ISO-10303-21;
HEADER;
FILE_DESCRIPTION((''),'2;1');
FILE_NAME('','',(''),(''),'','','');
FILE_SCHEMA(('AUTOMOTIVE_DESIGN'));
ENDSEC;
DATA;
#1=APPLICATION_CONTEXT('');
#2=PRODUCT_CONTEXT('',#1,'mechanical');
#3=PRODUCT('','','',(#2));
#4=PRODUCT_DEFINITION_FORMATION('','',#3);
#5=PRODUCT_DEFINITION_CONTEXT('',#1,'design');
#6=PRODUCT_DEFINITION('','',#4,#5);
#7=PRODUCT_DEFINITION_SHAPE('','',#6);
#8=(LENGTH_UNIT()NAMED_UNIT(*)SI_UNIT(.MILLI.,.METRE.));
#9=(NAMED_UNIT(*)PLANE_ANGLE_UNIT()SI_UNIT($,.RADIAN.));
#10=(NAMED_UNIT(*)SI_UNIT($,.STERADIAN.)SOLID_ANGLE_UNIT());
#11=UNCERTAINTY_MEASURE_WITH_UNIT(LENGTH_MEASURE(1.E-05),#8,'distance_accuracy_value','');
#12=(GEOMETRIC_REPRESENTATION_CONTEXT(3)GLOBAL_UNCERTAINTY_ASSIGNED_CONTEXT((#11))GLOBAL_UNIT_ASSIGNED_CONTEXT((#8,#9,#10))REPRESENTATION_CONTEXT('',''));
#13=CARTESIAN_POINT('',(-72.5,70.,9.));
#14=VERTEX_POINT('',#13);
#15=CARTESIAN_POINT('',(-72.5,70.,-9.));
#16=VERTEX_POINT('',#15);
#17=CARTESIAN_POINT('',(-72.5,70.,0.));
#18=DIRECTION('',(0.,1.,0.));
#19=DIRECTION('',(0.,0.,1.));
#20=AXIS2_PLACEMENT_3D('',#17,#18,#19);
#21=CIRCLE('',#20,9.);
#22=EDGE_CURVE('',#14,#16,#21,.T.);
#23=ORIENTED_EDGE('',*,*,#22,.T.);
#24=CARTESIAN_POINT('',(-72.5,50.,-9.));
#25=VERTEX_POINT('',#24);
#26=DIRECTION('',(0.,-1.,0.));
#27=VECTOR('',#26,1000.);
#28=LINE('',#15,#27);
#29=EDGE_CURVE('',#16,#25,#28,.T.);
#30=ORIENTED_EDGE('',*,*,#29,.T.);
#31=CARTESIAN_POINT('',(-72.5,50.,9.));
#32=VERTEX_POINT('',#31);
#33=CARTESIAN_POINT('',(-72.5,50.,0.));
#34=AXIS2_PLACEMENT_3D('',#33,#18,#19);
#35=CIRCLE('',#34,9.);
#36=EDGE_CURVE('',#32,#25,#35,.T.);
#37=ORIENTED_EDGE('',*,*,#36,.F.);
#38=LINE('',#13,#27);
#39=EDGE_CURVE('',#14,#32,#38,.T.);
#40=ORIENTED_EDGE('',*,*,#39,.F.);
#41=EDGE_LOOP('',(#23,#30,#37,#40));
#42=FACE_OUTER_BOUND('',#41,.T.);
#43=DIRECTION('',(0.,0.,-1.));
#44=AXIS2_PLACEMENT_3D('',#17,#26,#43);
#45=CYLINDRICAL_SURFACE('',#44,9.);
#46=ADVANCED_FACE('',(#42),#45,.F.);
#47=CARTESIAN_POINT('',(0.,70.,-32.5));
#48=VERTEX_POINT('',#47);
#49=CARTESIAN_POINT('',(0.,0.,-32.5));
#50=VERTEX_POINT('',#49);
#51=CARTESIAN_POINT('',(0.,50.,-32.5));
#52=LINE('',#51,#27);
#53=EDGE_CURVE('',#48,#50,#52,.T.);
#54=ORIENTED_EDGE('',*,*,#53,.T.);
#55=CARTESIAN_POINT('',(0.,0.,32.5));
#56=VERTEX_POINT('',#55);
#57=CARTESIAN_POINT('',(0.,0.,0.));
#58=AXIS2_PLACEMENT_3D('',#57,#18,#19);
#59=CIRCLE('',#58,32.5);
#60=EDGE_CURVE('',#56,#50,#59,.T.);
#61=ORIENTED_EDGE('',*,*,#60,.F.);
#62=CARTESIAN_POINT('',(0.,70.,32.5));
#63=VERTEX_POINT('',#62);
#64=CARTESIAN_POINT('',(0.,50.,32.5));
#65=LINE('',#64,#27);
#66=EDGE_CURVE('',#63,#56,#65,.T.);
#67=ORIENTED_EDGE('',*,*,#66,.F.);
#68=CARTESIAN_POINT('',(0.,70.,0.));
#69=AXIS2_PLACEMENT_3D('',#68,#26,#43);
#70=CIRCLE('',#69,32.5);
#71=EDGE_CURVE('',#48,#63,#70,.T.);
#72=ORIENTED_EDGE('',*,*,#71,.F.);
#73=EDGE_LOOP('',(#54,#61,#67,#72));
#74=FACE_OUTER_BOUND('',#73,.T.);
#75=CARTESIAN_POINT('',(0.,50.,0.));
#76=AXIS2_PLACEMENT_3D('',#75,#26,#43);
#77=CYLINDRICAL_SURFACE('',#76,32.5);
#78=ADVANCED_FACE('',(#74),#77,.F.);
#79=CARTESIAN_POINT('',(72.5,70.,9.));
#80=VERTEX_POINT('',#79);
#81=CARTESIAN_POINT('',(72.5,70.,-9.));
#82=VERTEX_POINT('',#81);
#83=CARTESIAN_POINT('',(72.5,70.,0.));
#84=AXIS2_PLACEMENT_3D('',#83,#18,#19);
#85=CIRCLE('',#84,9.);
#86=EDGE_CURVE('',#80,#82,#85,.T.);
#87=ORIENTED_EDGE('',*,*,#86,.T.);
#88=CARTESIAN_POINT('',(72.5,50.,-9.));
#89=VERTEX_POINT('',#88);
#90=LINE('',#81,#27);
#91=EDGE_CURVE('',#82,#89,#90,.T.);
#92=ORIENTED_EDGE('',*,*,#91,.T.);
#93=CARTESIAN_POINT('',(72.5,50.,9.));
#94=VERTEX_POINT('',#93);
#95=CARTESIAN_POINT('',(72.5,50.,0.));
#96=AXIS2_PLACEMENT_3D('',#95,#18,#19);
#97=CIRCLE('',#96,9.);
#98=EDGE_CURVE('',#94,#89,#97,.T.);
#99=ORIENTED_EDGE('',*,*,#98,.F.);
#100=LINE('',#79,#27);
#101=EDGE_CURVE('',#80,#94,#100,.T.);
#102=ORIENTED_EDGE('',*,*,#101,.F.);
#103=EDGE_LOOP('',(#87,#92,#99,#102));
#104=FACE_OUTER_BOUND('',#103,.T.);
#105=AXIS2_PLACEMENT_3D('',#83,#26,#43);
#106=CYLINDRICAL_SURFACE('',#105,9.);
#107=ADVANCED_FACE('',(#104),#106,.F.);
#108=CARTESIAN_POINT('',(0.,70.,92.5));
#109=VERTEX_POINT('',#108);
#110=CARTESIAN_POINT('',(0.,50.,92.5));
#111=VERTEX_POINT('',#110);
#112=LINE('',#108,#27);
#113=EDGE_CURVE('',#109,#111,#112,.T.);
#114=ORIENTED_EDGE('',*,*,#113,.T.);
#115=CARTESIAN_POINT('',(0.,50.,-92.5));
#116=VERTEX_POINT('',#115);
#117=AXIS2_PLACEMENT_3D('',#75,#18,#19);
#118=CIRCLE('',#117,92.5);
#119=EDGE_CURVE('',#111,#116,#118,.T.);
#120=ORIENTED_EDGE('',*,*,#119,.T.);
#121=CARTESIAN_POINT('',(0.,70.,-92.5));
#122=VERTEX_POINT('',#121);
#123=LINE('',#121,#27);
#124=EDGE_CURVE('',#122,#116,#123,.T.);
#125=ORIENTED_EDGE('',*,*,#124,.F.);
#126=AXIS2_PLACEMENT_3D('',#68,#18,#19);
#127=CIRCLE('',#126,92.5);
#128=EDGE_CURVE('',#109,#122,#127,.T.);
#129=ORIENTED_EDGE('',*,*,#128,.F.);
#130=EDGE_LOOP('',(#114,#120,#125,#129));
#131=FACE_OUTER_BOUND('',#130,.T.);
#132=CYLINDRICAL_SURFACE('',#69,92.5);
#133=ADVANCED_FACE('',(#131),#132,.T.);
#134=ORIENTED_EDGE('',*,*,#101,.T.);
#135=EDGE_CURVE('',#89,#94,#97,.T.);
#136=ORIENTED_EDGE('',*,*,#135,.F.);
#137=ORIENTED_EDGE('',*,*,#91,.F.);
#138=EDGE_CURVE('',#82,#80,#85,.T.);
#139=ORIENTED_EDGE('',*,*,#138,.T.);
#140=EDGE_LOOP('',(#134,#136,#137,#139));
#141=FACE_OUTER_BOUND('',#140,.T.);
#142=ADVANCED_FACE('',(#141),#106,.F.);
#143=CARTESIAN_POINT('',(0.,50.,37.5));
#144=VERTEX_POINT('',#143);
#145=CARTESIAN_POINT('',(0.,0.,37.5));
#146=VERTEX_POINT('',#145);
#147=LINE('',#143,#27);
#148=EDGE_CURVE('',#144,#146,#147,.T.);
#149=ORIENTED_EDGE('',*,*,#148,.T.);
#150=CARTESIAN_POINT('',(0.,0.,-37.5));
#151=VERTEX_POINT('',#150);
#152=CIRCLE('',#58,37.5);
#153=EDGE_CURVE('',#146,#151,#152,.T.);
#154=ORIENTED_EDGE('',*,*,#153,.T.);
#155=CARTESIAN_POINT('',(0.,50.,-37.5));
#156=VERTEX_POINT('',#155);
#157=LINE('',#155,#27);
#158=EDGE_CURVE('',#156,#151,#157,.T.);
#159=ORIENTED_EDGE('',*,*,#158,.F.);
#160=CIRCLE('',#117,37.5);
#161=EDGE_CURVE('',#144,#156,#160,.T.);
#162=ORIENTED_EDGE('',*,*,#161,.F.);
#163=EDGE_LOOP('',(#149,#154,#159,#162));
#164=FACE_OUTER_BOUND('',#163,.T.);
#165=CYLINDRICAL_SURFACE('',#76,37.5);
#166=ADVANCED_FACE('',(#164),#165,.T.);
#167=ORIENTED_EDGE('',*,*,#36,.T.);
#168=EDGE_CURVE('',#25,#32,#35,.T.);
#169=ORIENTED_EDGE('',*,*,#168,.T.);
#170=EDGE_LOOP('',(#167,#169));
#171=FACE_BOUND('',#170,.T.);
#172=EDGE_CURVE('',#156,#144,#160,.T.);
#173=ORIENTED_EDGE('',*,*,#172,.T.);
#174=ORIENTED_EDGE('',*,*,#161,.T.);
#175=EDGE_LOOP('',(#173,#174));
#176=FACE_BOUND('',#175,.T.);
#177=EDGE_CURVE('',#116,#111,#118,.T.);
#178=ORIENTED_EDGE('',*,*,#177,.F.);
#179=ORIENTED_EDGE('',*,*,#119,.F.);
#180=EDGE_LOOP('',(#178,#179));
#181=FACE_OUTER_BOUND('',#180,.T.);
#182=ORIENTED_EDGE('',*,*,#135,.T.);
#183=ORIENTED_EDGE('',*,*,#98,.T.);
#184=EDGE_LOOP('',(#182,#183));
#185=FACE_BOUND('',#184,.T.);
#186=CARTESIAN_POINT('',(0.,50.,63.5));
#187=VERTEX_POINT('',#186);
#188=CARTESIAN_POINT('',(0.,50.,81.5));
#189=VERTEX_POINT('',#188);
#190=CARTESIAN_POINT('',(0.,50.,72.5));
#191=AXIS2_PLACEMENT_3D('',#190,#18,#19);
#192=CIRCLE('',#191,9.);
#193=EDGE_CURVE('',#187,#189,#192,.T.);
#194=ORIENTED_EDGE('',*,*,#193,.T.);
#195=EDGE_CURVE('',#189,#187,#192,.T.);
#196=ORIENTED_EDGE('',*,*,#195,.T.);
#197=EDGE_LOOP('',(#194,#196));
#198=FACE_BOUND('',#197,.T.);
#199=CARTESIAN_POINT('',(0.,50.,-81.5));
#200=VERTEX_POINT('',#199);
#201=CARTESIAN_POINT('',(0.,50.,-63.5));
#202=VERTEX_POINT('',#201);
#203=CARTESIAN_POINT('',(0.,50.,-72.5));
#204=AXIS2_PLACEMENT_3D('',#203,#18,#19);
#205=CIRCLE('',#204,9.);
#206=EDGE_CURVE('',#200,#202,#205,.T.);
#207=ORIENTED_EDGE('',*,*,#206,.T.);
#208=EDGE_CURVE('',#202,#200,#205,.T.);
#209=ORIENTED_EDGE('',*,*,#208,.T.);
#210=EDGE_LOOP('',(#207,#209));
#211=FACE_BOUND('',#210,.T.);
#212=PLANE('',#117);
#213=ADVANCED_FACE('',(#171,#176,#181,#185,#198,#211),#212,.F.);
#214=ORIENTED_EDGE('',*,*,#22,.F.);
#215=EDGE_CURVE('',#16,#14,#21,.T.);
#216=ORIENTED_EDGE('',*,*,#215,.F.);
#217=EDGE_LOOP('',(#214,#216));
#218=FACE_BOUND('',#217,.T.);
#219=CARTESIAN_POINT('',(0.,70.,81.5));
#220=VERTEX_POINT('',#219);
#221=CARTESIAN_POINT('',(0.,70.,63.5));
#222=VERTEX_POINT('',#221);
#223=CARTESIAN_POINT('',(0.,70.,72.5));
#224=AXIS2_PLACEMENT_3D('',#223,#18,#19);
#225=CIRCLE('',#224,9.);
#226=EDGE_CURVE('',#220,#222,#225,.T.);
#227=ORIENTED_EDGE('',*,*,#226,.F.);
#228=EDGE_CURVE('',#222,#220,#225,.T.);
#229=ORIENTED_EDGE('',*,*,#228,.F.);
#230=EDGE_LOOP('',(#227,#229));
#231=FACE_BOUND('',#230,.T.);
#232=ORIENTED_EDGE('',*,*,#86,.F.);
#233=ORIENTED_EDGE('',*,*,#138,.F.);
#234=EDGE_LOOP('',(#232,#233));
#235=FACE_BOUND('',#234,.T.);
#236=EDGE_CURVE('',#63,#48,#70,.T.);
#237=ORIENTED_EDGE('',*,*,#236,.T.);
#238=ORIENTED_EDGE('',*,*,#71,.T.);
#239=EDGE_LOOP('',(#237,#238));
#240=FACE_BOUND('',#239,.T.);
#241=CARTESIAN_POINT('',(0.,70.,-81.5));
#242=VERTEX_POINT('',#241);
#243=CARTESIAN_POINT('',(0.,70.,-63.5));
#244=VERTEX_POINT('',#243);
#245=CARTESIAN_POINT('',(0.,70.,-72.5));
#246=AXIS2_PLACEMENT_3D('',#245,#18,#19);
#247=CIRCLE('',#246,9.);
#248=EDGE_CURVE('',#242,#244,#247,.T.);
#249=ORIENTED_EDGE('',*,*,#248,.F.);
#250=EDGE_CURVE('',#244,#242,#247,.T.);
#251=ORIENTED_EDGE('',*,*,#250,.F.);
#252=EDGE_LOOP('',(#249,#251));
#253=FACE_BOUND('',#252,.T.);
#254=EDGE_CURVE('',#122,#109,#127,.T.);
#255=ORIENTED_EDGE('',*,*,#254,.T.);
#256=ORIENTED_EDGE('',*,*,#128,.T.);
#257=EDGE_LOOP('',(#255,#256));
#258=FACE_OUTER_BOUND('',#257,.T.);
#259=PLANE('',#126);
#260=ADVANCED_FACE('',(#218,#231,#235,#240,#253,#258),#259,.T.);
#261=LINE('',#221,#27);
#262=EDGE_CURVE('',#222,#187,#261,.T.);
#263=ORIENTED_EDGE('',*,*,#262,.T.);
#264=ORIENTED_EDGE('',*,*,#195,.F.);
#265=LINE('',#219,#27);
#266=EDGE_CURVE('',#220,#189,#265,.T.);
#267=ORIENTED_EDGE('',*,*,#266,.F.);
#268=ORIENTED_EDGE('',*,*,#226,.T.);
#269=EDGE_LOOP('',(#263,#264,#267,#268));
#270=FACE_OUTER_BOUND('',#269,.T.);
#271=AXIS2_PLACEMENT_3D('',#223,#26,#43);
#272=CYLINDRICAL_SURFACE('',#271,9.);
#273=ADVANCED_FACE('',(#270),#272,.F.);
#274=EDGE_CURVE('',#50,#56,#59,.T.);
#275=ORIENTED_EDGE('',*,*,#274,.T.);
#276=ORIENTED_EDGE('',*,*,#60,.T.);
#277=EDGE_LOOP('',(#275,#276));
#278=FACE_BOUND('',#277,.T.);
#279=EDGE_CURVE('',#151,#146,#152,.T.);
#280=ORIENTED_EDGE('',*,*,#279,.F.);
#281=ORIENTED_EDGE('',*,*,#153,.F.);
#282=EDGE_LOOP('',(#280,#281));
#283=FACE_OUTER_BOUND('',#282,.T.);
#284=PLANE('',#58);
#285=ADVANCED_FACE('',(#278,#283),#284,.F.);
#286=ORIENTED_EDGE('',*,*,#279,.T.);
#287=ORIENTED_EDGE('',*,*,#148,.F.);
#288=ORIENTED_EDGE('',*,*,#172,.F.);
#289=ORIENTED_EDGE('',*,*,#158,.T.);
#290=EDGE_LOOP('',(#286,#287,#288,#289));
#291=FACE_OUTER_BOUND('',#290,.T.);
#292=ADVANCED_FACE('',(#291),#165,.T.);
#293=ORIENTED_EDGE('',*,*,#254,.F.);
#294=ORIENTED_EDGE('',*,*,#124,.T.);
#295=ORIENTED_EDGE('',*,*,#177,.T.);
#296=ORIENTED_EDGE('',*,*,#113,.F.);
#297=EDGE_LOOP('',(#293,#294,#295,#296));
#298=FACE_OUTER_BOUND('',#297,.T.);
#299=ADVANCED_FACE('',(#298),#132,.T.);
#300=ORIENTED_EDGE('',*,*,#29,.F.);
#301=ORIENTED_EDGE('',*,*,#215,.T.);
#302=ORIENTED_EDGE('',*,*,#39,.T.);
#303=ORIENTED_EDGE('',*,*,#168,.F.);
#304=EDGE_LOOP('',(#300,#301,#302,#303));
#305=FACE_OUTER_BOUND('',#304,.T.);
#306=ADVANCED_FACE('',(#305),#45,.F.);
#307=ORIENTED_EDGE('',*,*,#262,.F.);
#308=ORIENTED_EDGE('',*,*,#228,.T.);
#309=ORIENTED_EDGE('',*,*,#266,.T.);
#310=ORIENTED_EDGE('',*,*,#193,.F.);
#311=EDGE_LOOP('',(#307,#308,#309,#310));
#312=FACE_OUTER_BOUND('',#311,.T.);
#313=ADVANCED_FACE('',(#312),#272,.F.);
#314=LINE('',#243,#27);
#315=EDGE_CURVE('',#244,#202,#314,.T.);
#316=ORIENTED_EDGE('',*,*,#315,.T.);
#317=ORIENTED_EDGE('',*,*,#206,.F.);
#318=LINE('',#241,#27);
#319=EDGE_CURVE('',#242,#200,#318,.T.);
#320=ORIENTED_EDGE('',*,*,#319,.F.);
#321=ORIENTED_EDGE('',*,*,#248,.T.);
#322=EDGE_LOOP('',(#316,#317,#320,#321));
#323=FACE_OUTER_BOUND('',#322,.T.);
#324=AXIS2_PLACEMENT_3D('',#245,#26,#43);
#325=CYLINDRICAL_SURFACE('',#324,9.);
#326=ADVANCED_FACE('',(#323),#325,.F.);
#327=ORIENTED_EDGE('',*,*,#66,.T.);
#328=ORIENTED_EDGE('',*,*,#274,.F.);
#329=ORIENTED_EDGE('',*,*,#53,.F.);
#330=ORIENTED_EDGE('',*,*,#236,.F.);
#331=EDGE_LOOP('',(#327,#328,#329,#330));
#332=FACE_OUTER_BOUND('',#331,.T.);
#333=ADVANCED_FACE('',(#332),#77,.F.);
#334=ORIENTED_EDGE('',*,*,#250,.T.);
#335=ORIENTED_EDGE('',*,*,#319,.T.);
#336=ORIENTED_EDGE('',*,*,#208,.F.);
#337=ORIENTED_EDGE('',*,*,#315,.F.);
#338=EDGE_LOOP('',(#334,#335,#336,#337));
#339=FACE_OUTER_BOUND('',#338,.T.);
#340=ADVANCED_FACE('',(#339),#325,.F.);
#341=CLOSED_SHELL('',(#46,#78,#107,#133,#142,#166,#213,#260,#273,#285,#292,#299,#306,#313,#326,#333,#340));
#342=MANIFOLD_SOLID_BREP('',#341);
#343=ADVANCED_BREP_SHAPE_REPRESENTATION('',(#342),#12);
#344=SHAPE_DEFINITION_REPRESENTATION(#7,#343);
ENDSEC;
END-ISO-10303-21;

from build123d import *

# Parameters (mm, degrees)
SKETCH_1_R          = 37.5
SKETCH_1_R_2        = 32.5
EXTRUDE_1_DEPTH     = 50
SKETCH_2_R          = 92.5
SKETCH_2_R_2        = 37.5
SKETCH_2_R_3        = 9
EXTRUDE_2_DEPTH     = 20
SKETCH_3_R          = 37.5
EXTRUDE_3_DEPTH     = 20
SKETCH_4_R          = 32.5
CUT_EXTRUDE_1_DEPTH = 141.044635742


with BuildPart() as part:
    # 草图1 → 凸台-拉伸1 (new body)
    with BuildSketch(Plane(origin=(0, 0, 0), x_dir=(1, 0, 0), z_dir=(0, 1, 0))):
        with Locations(Location((0, 0, 0), (0, 0, 270))):
            Circle(SKETCH_1_R)
        with Locations(Location((0, 0, 0), (0, 0, 270))):
            Circle(SKETCH_1_R_2, mode=Mode.SUBTRACT)
    extrude(amount=EXTRUDE_1_DEPTH)



with BuildPart() as body_2:
    # 草图2 → 凸台-拉伸2 (new body)
    with BuildSketch(Plane(origin=(0, 50, 0), x_dir=(1, 0, 0), z_dir=(0, 1, 0))):
        with Locations(Location((0, 0, 0), (0, 0, 270))):
            Circle(SKETCH_2_R)
        with Locations(Location((0, 0, 0), (0, 0, 270))):
            Circle(SKETCH_2_R_2, mode=Mode.SUBTRACT)
        with Locations(Location((-72.5, 0, 0), (0, 0, 270))):
            Circle(SKETCH_2_R_3, mode=Mode.SUBTRACT)
        with Locations(Location((0, 72.5, 0), (0, 0, 270))):
            Circle(SKETCH_2_R_3, mode=Mode.SUBTRACT)
        with Locations(Location((72.5, 0, 0), (0, 0, 270))):
            Circle(SKETCH_2_R_3, mode=Mode.SUBTRACT)
        with Locations(Location((0, -72.5, 0), (0, 0, 270))):
            Circle(SKETCH_2_R_3, mode=Mode.SUBTRACT)
    extrude(amount=EXTRUDE_2_DEPTH)


with BuildPart() as part_1:
    add(part.part)

    add(body_2.part)  # 凸台-拉伸3 merges body 2
    # 草图3 → 凸台-拉伸3 (add)
    with BuildSketch(Plane(origin=(0, 50, 0), x_dir=(1, 0, 0), z_dir=(0, 1, 0))):
        with Locations(Location((0, 0, 0), (0, 0, 270))):
            Circle(SKETCH_3_R)
    extrude(amount=EXTRUDE_3_DEPTH)

    # 草图4 → 切除-拉伸1 (cut, through all)
    with BuildSketch(Plane.XZ.offset(-50)):
        with Locations(Location((0, 0, 0), (0, 0, 270))):
            Circle(SKETCH_4_R)
    extrude(amount=-CUT_EXTRUDE_1_DEPTH, mode=Mode.SUBTRACT)


solid = part_1.part
